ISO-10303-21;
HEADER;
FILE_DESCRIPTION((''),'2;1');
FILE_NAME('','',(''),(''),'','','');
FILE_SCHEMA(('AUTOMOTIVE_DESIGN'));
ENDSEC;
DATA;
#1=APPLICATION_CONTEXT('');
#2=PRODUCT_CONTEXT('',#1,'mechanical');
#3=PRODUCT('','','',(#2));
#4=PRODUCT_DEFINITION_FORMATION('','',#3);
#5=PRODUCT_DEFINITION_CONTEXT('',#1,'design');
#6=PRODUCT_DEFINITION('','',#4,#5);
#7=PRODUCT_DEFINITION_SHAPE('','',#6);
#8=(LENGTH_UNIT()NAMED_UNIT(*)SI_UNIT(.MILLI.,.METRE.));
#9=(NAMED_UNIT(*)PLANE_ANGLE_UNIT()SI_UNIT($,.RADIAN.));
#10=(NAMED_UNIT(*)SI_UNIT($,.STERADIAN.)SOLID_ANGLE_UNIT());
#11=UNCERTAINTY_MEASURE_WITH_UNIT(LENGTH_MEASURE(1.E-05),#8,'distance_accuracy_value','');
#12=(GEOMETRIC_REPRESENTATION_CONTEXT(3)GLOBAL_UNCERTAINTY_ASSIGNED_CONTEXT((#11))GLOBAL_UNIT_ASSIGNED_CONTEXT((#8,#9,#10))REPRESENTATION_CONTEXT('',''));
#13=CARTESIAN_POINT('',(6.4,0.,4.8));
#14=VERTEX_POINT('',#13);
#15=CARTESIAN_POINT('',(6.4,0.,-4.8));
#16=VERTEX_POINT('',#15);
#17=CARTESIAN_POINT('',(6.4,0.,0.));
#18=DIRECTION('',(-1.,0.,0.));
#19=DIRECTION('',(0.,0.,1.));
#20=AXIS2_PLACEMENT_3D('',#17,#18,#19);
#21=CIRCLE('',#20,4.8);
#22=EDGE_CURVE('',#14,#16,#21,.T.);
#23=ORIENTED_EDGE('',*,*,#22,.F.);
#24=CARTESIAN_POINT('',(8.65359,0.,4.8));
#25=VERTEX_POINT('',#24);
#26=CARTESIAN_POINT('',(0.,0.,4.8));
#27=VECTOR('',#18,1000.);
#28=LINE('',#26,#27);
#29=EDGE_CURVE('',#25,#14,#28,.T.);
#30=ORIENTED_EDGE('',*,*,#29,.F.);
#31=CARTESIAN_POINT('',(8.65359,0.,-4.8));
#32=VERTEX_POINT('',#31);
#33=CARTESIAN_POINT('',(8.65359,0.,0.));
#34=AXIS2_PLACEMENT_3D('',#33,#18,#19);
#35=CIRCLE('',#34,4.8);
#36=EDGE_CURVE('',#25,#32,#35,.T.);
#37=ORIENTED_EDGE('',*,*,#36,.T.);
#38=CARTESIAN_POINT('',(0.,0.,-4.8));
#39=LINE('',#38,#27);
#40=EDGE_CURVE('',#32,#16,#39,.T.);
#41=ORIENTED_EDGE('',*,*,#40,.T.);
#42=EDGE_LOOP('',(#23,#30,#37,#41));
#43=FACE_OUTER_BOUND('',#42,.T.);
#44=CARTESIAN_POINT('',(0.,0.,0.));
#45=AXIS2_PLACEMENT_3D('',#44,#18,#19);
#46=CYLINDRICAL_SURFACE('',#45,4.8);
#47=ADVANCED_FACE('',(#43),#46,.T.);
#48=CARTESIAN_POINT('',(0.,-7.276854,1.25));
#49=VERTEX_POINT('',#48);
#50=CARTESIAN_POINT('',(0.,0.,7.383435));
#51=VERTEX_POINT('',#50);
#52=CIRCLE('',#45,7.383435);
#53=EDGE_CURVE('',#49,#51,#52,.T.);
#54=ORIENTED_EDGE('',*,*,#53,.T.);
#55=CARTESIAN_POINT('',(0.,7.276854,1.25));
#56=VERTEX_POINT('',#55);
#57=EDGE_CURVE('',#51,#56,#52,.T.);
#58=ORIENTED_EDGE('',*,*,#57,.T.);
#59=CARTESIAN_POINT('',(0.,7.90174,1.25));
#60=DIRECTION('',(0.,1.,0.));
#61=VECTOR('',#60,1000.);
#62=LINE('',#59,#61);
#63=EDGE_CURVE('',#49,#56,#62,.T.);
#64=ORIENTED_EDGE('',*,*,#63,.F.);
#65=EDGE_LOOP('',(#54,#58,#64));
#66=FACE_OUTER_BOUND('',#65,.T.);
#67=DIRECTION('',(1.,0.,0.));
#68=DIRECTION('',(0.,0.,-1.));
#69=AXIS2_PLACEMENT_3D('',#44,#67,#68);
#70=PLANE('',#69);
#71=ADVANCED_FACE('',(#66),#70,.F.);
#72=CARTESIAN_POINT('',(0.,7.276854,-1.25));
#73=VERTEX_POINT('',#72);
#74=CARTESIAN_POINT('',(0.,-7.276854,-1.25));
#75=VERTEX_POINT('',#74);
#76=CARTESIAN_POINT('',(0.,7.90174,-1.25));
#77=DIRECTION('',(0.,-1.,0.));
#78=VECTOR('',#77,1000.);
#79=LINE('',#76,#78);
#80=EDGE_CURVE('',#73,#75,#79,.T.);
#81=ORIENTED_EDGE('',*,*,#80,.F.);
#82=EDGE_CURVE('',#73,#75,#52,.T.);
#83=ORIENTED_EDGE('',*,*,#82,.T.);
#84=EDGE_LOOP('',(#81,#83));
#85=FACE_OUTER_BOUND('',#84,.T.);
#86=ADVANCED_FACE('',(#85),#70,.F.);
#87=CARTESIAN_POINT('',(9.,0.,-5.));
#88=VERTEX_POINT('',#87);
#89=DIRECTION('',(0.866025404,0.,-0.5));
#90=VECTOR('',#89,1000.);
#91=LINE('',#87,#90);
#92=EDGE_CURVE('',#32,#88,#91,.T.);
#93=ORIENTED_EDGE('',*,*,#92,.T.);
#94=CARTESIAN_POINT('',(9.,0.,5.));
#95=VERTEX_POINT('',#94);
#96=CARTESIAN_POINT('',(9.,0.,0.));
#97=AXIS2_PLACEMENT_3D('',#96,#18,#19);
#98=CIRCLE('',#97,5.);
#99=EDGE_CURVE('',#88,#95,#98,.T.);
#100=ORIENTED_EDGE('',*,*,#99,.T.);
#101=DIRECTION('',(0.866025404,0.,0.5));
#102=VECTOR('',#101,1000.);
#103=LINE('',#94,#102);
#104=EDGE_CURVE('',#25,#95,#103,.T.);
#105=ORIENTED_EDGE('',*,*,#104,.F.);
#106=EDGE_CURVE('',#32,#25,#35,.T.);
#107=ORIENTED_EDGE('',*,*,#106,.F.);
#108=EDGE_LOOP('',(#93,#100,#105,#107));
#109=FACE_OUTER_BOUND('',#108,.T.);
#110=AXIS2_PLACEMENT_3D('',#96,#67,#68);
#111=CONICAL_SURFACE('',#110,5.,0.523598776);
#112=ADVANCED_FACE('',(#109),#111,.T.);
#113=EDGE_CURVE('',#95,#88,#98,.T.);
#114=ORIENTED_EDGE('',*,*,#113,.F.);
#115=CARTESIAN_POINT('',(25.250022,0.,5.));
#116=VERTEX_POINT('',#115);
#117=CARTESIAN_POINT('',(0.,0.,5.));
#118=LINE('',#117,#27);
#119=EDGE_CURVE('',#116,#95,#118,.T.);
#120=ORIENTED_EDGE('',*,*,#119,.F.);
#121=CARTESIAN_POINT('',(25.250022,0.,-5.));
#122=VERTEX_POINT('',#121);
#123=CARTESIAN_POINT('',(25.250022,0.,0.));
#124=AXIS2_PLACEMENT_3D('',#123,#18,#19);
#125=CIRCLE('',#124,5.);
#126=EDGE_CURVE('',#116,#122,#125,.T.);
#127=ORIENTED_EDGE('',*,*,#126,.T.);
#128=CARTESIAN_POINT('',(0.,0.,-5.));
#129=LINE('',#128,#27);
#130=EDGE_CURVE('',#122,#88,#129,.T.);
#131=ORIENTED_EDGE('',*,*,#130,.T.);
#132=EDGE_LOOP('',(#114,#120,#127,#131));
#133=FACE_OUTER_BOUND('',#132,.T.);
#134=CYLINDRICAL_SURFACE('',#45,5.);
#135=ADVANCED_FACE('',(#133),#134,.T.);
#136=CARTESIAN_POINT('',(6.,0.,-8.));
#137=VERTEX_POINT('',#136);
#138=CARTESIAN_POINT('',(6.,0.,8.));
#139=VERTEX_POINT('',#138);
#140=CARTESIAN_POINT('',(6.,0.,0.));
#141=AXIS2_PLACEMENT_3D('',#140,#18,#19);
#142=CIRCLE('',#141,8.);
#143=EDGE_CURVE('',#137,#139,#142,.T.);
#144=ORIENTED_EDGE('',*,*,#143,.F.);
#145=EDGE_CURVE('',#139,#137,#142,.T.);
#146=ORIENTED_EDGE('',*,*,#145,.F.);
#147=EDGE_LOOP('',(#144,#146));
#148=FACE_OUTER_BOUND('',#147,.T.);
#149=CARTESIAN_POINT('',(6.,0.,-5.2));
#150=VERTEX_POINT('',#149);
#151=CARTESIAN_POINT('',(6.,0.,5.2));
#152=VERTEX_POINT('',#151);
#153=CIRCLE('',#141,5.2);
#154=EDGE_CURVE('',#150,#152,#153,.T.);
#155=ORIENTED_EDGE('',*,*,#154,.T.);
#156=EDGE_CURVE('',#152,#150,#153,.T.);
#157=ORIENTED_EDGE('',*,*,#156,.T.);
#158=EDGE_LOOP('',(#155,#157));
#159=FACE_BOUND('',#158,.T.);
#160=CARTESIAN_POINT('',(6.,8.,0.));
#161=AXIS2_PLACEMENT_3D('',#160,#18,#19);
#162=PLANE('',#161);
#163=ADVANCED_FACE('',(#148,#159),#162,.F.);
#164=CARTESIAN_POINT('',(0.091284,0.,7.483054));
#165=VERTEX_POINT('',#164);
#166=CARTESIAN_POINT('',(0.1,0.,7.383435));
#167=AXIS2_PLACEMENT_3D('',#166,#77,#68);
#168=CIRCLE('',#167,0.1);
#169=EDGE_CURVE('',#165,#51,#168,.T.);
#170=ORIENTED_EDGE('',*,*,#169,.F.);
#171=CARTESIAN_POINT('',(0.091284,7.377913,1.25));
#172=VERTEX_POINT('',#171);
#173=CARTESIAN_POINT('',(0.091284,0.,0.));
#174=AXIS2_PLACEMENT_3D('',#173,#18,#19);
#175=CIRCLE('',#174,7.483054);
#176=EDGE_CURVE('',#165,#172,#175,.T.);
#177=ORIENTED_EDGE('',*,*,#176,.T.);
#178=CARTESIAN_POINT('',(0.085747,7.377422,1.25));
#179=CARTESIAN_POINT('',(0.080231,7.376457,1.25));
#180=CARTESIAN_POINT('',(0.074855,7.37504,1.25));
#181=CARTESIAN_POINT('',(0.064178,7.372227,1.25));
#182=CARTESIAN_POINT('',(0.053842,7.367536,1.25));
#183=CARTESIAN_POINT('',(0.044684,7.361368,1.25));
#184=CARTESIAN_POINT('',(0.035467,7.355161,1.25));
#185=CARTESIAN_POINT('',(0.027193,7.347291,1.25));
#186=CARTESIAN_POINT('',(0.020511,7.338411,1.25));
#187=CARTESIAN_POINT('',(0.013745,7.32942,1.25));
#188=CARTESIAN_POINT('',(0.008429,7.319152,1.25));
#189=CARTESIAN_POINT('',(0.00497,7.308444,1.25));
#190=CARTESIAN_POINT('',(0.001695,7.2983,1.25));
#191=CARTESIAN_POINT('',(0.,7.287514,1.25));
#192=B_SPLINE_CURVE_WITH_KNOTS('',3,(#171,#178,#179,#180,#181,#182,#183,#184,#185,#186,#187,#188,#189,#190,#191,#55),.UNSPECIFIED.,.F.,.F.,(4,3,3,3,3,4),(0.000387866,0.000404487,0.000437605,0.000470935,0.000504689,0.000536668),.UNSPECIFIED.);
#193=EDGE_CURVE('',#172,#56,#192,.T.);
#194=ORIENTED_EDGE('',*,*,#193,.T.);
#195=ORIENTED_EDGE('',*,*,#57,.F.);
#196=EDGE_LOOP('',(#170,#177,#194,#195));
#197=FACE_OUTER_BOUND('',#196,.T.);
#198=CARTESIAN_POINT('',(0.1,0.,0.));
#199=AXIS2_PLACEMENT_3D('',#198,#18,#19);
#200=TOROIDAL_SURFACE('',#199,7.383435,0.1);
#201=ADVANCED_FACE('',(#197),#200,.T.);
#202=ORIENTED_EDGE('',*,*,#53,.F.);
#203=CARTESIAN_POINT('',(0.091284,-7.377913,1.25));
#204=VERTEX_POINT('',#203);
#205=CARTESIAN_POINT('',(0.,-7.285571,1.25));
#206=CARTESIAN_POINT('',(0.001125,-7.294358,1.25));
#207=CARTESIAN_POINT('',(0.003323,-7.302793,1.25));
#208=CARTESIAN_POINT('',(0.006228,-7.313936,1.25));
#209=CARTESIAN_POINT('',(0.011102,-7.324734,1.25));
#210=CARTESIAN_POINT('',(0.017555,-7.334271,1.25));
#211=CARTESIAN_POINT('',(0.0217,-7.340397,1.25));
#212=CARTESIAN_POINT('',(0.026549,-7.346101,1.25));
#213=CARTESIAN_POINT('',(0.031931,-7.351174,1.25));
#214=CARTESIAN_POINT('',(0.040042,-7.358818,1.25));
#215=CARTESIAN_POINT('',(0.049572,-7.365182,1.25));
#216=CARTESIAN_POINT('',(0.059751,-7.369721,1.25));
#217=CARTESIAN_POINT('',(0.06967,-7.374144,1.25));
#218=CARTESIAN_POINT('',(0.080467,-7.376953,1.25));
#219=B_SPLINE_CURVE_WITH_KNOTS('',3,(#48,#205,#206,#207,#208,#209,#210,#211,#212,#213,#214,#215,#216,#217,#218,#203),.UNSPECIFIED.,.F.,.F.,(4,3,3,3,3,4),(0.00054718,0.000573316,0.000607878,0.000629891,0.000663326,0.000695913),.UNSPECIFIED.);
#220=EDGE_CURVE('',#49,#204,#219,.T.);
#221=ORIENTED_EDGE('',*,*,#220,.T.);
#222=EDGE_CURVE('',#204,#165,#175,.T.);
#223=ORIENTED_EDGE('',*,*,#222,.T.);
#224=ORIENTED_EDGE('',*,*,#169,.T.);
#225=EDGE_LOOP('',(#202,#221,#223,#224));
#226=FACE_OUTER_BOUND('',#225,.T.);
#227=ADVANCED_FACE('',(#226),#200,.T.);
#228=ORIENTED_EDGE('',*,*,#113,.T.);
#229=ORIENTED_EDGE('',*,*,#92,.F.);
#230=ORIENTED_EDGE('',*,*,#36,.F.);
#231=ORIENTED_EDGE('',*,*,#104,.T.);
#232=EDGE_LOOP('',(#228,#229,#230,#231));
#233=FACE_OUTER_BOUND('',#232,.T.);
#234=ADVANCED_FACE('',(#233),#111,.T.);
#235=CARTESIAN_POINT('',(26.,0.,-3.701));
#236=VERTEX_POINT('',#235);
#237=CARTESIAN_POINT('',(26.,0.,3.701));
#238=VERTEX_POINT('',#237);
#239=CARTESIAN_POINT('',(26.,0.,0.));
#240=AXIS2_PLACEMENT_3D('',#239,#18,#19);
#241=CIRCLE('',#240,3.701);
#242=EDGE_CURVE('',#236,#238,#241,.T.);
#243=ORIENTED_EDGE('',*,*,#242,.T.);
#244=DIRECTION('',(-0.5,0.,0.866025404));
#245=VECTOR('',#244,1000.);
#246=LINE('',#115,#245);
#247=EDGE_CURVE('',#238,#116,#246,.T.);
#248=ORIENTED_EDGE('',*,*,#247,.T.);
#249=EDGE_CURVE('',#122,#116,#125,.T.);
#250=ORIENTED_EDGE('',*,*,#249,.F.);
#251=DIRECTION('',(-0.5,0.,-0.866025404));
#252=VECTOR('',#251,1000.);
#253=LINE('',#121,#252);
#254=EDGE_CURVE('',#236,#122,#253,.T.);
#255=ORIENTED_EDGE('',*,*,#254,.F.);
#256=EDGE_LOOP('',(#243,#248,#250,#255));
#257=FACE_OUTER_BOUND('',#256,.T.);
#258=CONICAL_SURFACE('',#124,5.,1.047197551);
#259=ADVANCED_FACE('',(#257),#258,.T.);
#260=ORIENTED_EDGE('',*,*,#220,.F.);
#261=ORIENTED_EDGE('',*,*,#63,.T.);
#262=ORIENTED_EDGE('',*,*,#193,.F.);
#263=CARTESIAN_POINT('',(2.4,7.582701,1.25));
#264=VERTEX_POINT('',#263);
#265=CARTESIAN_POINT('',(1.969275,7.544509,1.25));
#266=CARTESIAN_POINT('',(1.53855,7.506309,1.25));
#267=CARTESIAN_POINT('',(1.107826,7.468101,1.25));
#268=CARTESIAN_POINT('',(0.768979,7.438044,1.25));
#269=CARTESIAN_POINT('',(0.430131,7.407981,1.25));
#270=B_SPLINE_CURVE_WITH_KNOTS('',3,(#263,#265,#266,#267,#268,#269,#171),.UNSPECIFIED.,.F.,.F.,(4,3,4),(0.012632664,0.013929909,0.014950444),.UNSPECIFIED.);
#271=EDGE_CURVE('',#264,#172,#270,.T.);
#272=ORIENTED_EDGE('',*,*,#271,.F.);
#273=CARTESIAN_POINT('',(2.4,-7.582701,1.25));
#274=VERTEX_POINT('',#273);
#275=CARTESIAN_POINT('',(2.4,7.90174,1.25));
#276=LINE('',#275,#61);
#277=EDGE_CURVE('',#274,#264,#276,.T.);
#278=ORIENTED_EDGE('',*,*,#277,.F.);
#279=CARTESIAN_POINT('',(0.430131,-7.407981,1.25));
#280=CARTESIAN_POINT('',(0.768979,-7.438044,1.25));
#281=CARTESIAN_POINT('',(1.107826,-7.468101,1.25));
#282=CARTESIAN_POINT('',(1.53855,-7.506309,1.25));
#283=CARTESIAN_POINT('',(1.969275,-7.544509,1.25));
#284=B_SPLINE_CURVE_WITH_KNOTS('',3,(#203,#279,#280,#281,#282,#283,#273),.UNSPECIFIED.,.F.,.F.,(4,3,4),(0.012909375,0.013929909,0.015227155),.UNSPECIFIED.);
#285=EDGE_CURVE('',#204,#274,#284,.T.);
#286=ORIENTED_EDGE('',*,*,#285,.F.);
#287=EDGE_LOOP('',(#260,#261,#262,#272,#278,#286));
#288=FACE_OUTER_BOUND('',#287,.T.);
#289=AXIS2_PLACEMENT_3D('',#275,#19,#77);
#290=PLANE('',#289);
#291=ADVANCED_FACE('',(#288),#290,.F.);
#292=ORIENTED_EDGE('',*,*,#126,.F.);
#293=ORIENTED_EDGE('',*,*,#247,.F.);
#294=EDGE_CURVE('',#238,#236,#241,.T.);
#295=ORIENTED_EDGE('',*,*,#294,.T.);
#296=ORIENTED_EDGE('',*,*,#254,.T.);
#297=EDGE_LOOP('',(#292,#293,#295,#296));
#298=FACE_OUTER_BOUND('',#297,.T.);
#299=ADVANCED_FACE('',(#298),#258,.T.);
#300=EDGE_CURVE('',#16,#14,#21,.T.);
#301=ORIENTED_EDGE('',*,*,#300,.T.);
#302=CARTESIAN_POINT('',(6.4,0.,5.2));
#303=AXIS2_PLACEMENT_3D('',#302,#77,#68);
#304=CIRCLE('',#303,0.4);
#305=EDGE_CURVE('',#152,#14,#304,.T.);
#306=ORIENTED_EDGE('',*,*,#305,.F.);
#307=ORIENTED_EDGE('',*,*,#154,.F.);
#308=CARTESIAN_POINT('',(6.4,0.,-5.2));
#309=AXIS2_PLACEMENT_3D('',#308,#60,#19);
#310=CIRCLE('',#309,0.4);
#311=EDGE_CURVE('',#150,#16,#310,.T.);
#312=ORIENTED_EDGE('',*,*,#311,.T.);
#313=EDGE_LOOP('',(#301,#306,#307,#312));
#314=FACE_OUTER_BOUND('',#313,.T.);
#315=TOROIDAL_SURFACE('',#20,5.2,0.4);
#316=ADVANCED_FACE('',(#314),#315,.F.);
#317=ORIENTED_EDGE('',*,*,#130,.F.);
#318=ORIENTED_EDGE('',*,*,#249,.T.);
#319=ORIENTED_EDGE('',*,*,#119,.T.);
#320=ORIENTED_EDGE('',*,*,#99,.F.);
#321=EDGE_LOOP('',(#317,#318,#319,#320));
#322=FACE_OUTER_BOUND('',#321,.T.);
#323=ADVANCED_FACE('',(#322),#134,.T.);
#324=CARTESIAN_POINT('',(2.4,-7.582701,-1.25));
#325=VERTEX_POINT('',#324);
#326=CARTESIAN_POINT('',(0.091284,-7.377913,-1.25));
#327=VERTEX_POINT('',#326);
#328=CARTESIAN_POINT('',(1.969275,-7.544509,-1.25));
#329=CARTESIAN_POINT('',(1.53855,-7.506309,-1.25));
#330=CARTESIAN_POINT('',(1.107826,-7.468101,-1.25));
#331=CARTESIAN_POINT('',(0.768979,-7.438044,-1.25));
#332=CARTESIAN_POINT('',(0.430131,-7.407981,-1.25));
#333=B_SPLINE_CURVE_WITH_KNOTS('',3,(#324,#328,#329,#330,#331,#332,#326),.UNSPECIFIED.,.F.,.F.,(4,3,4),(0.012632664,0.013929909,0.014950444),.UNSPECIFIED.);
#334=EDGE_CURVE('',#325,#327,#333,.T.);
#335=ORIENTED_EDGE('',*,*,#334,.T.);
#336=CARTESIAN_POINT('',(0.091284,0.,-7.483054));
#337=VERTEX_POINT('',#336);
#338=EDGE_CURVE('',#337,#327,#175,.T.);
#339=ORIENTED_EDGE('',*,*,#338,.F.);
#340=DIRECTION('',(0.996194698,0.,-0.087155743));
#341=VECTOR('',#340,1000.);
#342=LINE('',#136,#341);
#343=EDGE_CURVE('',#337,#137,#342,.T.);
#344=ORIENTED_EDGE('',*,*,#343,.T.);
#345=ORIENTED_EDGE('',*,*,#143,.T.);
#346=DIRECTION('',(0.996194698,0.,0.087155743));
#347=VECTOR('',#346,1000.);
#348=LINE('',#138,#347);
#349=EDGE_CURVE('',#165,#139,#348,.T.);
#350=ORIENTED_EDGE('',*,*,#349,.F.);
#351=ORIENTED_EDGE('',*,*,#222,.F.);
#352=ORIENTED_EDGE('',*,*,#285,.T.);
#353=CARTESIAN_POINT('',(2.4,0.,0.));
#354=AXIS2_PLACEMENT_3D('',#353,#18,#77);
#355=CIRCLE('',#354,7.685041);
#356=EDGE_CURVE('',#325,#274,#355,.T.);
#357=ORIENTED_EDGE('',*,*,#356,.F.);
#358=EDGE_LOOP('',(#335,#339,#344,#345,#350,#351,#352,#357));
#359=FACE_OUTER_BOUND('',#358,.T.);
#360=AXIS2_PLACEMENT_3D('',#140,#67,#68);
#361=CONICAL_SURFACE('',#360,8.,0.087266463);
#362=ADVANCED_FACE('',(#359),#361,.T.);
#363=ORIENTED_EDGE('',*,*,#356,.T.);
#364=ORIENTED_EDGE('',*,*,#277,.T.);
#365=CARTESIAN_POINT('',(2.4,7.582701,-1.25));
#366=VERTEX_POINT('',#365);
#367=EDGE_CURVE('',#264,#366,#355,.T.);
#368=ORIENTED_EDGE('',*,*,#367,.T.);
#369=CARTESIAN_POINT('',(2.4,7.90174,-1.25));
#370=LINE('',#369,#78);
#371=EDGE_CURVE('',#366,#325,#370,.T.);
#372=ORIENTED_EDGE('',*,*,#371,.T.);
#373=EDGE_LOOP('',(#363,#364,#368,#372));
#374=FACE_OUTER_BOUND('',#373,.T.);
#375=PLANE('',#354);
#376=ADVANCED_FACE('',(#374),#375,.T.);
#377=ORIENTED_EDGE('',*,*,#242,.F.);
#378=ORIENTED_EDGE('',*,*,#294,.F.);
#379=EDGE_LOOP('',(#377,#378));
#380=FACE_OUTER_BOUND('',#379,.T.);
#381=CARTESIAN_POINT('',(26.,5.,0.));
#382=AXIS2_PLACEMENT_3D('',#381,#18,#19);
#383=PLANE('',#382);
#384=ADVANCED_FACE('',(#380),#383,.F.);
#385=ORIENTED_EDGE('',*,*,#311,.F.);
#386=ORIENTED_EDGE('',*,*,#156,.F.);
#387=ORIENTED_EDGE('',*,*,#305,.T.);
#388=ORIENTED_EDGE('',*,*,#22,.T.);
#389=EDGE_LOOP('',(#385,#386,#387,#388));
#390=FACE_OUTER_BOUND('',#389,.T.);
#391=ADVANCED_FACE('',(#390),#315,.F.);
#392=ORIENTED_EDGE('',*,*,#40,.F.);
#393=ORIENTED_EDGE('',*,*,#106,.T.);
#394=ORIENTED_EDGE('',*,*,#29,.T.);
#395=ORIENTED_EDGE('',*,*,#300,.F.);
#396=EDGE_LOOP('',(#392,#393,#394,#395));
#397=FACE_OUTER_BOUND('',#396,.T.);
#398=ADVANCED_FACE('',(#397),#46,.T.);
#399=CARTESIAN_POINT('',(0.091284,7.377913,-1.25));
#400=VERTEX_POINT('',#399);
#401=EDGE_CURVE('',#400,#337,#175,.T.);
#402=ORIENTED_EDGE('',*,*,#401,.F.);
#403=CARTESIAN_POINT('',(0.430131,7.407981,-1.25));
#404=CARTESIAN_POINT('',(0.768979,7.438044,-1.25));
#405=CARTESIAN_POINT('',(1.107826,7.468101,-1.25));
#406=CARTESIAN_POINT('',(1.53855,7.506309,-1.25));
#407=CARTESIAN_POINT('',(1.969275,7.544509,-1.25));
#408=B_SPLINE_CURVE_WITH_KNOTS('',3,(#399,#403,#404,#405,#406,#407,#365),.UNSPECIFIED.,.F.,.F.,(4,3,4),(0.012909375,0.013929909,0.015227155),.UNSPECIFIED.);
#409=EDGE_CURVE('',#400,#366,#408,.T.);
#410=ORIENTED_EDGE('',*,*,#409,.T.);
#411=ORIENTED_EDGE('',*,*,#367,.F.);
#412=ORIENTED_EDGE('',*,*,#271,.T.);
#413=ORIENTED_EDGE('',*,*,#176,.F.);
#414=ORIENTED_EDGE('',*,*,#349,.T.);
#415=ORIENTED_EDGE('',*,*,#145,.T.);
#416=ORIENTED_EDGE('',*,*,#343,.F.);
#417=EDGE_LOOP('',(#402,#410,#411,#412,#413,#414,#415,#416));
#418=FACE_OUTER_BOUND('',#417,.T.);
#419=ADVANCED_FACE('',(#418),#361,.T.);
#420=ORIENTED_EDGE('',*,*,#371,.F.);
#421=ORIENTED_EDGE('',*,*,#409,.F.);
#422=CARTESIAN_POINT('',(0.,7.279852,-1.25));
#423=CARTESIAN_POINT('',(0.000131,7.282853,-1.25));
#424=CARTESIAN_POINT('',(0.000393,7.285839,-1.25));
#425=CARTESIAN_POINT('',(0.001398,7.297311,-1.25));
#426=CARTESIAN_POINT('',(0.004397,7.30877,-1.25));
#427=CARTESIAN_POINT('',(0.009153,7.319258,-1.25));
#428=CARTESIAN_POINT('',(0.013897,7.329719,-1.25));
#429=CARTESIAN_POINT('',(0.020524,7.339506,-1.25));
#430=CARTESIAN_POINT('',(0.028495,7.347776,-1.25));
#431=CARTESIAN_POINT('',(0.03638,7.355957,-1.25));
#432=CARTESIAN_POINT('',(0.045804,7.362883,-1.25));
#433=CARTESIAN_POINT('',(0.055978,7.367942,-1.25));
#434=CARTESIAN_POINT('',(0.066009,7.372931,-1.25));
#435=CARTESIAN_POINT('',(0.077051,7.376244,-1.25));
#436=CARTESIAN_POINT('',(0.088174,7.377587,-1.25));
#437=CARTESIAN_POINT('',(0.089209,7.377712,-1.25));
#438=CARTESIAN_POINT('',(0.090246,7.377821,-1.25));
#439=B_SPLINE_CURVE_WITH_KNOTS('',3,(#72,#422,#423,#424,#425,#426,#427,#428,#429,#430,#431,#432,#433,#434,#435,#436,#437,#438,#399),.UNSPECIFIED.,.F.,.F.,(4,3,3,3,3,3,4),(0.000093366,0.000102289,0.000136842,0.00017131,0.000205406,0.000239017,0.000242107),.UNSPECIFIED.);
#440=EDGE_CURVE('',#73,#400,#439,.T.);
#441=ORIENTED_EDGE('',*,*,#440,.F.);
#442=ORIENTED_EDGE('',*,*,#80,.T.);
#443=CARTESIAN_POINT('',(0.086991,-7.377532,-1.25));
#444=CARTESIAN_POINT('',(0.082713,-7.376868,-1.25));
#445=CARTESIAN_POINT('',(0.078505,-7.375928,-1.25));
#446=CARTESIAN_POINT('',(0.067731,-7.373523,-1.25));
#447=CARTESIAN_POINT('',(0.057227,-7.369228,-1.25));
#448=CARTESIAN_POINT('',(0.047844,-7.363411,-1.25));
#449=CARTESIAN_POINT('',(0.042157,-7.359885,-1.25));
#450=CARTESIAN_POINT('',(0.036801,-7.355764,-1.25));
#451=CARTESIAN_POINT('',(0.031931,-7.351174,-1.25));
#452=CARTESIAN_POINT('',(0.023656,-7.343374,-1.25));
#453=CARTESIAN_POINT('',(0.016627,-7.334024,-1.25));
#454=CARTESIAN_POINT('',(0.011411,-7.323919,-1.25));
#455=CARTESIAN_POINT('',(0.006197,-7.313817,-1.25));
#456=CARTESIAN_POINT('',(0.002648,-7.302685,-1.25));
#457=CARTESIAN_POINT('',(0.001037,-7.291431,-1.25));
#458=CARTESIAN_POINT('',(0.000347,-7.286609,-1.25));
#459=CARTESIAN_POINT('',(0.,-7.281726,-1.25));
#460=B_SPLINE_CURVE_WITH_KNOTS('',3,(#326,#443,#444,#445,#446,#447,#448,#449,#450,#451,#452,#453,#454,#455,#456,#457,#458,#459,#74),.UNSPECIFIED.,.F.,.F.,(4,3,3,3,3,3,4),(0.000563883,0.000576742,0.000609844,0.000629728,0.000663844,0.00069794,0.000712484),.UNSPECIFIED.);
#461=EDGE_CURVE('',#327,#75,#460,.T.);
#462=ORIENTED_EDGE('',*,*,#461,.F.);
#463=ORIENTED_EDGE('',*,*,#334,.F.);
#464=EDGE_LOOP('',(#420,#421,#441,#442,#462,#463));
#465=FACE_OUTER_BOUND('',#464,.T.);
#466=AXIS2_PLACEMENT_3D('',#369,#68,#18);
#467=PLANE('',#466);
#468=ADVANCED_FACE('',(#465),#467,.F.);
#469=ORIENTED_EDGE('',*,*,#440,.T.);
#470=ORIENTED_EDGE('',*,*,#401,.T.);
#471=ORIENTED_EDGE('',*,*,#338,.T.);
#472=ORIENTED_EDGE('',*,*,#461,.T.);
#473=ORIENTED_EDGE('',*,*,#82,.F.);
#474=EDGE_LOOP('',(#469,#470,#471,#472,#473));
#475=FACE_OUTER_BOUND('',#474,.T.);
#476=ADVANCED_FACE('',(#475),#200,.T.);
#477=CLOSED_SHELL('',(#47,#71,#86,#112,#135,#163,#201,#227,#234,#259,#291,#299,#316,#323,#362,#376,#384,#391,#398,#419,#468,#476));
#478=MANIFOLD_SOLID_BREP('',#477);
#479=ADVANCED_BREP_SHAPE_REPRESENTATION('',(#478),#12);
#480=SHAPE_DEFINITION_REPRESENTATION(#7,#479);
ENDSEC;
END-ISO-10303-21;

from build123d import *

# Parameters (mm, degrees)
CUT_EXTRUDE_1_DEPTH = 2.4


with BuildPart() as part:
    # 草图1 → Revolve 665 (revolve)
    with BuildSketch(Plane.XY, mode=Mode.PRIVATE) as revolve_665_sk:
        with BuildLine():
            Line((0, 0), (0, 7.383434901))
            ThreePointArc((0, 7.383434901), (0.026272266, 7.450993922), (0.091284426, 7.483054371))
            Line((0.091284426, 7.483054371), (6, 8))
            Line((6, 8), (6, 5.2))
            ThreePointArc((6, 5.2), (6.117157288, 4.917157288), (6.4, 4.8))
            Line((6.4, 4.8), (8.653589838, 4.8))
            Line((8.653589838, 4.8), (9, 5))
            Line((9, 5), (26, 5))
            Line((26, 5), (26, 0))
            Line((26, 0), (0, 0))
        make_face()
    revolve(revolve_665_sk.sketch.rotate(Axis((0, 0, 0), (1, 0, 0)), 90), axis=Axis((0, 0, 0), (1, 0, 0)))

    # 草图2 → 切除-拉伸1 (cut)
    with BuildSketch(Plane.ZY):
        with BuildLine():
            Line((1.25, 7.901740315), (1.25, -7.901740315))
            ThreePointArc((1.25, -7.901740315), (0, -8), (-1.25, -7.901740315))
            Line((-1.25, -7.901740315), (-1.25, 7.901740315))
            ThreePointArc((-1.25, 7.901740315), (0, 8), (1.25, 7.901740315))
        make_face()
    extrude(amount=-CUT_EXTRUDE_1_DEPTH, mode=Mode.SUBTRACT)

    # 草图3 → 切除-旋转1 (revolve, cut)
    with BuildSketch(Plane(origin=(0, 0, 0), x_dir=(1, 0, 0), z_dir=(0, 1, 0)), mode=Mode.PRIVATE) as cut_revolve_1_sk:
        Polygon((25.250022, 5), (26.749978, 5), (26, 3.701), align=None)
    revolve(cut_revolve_1_sk.sketch.rotate(Axis((0, 0, 0), (1, 0, 0)), 180), axis=Axis((0, 0, 0), (1, 0, 0)), mode=Mode.SUBTRACT)


solid = part.part
